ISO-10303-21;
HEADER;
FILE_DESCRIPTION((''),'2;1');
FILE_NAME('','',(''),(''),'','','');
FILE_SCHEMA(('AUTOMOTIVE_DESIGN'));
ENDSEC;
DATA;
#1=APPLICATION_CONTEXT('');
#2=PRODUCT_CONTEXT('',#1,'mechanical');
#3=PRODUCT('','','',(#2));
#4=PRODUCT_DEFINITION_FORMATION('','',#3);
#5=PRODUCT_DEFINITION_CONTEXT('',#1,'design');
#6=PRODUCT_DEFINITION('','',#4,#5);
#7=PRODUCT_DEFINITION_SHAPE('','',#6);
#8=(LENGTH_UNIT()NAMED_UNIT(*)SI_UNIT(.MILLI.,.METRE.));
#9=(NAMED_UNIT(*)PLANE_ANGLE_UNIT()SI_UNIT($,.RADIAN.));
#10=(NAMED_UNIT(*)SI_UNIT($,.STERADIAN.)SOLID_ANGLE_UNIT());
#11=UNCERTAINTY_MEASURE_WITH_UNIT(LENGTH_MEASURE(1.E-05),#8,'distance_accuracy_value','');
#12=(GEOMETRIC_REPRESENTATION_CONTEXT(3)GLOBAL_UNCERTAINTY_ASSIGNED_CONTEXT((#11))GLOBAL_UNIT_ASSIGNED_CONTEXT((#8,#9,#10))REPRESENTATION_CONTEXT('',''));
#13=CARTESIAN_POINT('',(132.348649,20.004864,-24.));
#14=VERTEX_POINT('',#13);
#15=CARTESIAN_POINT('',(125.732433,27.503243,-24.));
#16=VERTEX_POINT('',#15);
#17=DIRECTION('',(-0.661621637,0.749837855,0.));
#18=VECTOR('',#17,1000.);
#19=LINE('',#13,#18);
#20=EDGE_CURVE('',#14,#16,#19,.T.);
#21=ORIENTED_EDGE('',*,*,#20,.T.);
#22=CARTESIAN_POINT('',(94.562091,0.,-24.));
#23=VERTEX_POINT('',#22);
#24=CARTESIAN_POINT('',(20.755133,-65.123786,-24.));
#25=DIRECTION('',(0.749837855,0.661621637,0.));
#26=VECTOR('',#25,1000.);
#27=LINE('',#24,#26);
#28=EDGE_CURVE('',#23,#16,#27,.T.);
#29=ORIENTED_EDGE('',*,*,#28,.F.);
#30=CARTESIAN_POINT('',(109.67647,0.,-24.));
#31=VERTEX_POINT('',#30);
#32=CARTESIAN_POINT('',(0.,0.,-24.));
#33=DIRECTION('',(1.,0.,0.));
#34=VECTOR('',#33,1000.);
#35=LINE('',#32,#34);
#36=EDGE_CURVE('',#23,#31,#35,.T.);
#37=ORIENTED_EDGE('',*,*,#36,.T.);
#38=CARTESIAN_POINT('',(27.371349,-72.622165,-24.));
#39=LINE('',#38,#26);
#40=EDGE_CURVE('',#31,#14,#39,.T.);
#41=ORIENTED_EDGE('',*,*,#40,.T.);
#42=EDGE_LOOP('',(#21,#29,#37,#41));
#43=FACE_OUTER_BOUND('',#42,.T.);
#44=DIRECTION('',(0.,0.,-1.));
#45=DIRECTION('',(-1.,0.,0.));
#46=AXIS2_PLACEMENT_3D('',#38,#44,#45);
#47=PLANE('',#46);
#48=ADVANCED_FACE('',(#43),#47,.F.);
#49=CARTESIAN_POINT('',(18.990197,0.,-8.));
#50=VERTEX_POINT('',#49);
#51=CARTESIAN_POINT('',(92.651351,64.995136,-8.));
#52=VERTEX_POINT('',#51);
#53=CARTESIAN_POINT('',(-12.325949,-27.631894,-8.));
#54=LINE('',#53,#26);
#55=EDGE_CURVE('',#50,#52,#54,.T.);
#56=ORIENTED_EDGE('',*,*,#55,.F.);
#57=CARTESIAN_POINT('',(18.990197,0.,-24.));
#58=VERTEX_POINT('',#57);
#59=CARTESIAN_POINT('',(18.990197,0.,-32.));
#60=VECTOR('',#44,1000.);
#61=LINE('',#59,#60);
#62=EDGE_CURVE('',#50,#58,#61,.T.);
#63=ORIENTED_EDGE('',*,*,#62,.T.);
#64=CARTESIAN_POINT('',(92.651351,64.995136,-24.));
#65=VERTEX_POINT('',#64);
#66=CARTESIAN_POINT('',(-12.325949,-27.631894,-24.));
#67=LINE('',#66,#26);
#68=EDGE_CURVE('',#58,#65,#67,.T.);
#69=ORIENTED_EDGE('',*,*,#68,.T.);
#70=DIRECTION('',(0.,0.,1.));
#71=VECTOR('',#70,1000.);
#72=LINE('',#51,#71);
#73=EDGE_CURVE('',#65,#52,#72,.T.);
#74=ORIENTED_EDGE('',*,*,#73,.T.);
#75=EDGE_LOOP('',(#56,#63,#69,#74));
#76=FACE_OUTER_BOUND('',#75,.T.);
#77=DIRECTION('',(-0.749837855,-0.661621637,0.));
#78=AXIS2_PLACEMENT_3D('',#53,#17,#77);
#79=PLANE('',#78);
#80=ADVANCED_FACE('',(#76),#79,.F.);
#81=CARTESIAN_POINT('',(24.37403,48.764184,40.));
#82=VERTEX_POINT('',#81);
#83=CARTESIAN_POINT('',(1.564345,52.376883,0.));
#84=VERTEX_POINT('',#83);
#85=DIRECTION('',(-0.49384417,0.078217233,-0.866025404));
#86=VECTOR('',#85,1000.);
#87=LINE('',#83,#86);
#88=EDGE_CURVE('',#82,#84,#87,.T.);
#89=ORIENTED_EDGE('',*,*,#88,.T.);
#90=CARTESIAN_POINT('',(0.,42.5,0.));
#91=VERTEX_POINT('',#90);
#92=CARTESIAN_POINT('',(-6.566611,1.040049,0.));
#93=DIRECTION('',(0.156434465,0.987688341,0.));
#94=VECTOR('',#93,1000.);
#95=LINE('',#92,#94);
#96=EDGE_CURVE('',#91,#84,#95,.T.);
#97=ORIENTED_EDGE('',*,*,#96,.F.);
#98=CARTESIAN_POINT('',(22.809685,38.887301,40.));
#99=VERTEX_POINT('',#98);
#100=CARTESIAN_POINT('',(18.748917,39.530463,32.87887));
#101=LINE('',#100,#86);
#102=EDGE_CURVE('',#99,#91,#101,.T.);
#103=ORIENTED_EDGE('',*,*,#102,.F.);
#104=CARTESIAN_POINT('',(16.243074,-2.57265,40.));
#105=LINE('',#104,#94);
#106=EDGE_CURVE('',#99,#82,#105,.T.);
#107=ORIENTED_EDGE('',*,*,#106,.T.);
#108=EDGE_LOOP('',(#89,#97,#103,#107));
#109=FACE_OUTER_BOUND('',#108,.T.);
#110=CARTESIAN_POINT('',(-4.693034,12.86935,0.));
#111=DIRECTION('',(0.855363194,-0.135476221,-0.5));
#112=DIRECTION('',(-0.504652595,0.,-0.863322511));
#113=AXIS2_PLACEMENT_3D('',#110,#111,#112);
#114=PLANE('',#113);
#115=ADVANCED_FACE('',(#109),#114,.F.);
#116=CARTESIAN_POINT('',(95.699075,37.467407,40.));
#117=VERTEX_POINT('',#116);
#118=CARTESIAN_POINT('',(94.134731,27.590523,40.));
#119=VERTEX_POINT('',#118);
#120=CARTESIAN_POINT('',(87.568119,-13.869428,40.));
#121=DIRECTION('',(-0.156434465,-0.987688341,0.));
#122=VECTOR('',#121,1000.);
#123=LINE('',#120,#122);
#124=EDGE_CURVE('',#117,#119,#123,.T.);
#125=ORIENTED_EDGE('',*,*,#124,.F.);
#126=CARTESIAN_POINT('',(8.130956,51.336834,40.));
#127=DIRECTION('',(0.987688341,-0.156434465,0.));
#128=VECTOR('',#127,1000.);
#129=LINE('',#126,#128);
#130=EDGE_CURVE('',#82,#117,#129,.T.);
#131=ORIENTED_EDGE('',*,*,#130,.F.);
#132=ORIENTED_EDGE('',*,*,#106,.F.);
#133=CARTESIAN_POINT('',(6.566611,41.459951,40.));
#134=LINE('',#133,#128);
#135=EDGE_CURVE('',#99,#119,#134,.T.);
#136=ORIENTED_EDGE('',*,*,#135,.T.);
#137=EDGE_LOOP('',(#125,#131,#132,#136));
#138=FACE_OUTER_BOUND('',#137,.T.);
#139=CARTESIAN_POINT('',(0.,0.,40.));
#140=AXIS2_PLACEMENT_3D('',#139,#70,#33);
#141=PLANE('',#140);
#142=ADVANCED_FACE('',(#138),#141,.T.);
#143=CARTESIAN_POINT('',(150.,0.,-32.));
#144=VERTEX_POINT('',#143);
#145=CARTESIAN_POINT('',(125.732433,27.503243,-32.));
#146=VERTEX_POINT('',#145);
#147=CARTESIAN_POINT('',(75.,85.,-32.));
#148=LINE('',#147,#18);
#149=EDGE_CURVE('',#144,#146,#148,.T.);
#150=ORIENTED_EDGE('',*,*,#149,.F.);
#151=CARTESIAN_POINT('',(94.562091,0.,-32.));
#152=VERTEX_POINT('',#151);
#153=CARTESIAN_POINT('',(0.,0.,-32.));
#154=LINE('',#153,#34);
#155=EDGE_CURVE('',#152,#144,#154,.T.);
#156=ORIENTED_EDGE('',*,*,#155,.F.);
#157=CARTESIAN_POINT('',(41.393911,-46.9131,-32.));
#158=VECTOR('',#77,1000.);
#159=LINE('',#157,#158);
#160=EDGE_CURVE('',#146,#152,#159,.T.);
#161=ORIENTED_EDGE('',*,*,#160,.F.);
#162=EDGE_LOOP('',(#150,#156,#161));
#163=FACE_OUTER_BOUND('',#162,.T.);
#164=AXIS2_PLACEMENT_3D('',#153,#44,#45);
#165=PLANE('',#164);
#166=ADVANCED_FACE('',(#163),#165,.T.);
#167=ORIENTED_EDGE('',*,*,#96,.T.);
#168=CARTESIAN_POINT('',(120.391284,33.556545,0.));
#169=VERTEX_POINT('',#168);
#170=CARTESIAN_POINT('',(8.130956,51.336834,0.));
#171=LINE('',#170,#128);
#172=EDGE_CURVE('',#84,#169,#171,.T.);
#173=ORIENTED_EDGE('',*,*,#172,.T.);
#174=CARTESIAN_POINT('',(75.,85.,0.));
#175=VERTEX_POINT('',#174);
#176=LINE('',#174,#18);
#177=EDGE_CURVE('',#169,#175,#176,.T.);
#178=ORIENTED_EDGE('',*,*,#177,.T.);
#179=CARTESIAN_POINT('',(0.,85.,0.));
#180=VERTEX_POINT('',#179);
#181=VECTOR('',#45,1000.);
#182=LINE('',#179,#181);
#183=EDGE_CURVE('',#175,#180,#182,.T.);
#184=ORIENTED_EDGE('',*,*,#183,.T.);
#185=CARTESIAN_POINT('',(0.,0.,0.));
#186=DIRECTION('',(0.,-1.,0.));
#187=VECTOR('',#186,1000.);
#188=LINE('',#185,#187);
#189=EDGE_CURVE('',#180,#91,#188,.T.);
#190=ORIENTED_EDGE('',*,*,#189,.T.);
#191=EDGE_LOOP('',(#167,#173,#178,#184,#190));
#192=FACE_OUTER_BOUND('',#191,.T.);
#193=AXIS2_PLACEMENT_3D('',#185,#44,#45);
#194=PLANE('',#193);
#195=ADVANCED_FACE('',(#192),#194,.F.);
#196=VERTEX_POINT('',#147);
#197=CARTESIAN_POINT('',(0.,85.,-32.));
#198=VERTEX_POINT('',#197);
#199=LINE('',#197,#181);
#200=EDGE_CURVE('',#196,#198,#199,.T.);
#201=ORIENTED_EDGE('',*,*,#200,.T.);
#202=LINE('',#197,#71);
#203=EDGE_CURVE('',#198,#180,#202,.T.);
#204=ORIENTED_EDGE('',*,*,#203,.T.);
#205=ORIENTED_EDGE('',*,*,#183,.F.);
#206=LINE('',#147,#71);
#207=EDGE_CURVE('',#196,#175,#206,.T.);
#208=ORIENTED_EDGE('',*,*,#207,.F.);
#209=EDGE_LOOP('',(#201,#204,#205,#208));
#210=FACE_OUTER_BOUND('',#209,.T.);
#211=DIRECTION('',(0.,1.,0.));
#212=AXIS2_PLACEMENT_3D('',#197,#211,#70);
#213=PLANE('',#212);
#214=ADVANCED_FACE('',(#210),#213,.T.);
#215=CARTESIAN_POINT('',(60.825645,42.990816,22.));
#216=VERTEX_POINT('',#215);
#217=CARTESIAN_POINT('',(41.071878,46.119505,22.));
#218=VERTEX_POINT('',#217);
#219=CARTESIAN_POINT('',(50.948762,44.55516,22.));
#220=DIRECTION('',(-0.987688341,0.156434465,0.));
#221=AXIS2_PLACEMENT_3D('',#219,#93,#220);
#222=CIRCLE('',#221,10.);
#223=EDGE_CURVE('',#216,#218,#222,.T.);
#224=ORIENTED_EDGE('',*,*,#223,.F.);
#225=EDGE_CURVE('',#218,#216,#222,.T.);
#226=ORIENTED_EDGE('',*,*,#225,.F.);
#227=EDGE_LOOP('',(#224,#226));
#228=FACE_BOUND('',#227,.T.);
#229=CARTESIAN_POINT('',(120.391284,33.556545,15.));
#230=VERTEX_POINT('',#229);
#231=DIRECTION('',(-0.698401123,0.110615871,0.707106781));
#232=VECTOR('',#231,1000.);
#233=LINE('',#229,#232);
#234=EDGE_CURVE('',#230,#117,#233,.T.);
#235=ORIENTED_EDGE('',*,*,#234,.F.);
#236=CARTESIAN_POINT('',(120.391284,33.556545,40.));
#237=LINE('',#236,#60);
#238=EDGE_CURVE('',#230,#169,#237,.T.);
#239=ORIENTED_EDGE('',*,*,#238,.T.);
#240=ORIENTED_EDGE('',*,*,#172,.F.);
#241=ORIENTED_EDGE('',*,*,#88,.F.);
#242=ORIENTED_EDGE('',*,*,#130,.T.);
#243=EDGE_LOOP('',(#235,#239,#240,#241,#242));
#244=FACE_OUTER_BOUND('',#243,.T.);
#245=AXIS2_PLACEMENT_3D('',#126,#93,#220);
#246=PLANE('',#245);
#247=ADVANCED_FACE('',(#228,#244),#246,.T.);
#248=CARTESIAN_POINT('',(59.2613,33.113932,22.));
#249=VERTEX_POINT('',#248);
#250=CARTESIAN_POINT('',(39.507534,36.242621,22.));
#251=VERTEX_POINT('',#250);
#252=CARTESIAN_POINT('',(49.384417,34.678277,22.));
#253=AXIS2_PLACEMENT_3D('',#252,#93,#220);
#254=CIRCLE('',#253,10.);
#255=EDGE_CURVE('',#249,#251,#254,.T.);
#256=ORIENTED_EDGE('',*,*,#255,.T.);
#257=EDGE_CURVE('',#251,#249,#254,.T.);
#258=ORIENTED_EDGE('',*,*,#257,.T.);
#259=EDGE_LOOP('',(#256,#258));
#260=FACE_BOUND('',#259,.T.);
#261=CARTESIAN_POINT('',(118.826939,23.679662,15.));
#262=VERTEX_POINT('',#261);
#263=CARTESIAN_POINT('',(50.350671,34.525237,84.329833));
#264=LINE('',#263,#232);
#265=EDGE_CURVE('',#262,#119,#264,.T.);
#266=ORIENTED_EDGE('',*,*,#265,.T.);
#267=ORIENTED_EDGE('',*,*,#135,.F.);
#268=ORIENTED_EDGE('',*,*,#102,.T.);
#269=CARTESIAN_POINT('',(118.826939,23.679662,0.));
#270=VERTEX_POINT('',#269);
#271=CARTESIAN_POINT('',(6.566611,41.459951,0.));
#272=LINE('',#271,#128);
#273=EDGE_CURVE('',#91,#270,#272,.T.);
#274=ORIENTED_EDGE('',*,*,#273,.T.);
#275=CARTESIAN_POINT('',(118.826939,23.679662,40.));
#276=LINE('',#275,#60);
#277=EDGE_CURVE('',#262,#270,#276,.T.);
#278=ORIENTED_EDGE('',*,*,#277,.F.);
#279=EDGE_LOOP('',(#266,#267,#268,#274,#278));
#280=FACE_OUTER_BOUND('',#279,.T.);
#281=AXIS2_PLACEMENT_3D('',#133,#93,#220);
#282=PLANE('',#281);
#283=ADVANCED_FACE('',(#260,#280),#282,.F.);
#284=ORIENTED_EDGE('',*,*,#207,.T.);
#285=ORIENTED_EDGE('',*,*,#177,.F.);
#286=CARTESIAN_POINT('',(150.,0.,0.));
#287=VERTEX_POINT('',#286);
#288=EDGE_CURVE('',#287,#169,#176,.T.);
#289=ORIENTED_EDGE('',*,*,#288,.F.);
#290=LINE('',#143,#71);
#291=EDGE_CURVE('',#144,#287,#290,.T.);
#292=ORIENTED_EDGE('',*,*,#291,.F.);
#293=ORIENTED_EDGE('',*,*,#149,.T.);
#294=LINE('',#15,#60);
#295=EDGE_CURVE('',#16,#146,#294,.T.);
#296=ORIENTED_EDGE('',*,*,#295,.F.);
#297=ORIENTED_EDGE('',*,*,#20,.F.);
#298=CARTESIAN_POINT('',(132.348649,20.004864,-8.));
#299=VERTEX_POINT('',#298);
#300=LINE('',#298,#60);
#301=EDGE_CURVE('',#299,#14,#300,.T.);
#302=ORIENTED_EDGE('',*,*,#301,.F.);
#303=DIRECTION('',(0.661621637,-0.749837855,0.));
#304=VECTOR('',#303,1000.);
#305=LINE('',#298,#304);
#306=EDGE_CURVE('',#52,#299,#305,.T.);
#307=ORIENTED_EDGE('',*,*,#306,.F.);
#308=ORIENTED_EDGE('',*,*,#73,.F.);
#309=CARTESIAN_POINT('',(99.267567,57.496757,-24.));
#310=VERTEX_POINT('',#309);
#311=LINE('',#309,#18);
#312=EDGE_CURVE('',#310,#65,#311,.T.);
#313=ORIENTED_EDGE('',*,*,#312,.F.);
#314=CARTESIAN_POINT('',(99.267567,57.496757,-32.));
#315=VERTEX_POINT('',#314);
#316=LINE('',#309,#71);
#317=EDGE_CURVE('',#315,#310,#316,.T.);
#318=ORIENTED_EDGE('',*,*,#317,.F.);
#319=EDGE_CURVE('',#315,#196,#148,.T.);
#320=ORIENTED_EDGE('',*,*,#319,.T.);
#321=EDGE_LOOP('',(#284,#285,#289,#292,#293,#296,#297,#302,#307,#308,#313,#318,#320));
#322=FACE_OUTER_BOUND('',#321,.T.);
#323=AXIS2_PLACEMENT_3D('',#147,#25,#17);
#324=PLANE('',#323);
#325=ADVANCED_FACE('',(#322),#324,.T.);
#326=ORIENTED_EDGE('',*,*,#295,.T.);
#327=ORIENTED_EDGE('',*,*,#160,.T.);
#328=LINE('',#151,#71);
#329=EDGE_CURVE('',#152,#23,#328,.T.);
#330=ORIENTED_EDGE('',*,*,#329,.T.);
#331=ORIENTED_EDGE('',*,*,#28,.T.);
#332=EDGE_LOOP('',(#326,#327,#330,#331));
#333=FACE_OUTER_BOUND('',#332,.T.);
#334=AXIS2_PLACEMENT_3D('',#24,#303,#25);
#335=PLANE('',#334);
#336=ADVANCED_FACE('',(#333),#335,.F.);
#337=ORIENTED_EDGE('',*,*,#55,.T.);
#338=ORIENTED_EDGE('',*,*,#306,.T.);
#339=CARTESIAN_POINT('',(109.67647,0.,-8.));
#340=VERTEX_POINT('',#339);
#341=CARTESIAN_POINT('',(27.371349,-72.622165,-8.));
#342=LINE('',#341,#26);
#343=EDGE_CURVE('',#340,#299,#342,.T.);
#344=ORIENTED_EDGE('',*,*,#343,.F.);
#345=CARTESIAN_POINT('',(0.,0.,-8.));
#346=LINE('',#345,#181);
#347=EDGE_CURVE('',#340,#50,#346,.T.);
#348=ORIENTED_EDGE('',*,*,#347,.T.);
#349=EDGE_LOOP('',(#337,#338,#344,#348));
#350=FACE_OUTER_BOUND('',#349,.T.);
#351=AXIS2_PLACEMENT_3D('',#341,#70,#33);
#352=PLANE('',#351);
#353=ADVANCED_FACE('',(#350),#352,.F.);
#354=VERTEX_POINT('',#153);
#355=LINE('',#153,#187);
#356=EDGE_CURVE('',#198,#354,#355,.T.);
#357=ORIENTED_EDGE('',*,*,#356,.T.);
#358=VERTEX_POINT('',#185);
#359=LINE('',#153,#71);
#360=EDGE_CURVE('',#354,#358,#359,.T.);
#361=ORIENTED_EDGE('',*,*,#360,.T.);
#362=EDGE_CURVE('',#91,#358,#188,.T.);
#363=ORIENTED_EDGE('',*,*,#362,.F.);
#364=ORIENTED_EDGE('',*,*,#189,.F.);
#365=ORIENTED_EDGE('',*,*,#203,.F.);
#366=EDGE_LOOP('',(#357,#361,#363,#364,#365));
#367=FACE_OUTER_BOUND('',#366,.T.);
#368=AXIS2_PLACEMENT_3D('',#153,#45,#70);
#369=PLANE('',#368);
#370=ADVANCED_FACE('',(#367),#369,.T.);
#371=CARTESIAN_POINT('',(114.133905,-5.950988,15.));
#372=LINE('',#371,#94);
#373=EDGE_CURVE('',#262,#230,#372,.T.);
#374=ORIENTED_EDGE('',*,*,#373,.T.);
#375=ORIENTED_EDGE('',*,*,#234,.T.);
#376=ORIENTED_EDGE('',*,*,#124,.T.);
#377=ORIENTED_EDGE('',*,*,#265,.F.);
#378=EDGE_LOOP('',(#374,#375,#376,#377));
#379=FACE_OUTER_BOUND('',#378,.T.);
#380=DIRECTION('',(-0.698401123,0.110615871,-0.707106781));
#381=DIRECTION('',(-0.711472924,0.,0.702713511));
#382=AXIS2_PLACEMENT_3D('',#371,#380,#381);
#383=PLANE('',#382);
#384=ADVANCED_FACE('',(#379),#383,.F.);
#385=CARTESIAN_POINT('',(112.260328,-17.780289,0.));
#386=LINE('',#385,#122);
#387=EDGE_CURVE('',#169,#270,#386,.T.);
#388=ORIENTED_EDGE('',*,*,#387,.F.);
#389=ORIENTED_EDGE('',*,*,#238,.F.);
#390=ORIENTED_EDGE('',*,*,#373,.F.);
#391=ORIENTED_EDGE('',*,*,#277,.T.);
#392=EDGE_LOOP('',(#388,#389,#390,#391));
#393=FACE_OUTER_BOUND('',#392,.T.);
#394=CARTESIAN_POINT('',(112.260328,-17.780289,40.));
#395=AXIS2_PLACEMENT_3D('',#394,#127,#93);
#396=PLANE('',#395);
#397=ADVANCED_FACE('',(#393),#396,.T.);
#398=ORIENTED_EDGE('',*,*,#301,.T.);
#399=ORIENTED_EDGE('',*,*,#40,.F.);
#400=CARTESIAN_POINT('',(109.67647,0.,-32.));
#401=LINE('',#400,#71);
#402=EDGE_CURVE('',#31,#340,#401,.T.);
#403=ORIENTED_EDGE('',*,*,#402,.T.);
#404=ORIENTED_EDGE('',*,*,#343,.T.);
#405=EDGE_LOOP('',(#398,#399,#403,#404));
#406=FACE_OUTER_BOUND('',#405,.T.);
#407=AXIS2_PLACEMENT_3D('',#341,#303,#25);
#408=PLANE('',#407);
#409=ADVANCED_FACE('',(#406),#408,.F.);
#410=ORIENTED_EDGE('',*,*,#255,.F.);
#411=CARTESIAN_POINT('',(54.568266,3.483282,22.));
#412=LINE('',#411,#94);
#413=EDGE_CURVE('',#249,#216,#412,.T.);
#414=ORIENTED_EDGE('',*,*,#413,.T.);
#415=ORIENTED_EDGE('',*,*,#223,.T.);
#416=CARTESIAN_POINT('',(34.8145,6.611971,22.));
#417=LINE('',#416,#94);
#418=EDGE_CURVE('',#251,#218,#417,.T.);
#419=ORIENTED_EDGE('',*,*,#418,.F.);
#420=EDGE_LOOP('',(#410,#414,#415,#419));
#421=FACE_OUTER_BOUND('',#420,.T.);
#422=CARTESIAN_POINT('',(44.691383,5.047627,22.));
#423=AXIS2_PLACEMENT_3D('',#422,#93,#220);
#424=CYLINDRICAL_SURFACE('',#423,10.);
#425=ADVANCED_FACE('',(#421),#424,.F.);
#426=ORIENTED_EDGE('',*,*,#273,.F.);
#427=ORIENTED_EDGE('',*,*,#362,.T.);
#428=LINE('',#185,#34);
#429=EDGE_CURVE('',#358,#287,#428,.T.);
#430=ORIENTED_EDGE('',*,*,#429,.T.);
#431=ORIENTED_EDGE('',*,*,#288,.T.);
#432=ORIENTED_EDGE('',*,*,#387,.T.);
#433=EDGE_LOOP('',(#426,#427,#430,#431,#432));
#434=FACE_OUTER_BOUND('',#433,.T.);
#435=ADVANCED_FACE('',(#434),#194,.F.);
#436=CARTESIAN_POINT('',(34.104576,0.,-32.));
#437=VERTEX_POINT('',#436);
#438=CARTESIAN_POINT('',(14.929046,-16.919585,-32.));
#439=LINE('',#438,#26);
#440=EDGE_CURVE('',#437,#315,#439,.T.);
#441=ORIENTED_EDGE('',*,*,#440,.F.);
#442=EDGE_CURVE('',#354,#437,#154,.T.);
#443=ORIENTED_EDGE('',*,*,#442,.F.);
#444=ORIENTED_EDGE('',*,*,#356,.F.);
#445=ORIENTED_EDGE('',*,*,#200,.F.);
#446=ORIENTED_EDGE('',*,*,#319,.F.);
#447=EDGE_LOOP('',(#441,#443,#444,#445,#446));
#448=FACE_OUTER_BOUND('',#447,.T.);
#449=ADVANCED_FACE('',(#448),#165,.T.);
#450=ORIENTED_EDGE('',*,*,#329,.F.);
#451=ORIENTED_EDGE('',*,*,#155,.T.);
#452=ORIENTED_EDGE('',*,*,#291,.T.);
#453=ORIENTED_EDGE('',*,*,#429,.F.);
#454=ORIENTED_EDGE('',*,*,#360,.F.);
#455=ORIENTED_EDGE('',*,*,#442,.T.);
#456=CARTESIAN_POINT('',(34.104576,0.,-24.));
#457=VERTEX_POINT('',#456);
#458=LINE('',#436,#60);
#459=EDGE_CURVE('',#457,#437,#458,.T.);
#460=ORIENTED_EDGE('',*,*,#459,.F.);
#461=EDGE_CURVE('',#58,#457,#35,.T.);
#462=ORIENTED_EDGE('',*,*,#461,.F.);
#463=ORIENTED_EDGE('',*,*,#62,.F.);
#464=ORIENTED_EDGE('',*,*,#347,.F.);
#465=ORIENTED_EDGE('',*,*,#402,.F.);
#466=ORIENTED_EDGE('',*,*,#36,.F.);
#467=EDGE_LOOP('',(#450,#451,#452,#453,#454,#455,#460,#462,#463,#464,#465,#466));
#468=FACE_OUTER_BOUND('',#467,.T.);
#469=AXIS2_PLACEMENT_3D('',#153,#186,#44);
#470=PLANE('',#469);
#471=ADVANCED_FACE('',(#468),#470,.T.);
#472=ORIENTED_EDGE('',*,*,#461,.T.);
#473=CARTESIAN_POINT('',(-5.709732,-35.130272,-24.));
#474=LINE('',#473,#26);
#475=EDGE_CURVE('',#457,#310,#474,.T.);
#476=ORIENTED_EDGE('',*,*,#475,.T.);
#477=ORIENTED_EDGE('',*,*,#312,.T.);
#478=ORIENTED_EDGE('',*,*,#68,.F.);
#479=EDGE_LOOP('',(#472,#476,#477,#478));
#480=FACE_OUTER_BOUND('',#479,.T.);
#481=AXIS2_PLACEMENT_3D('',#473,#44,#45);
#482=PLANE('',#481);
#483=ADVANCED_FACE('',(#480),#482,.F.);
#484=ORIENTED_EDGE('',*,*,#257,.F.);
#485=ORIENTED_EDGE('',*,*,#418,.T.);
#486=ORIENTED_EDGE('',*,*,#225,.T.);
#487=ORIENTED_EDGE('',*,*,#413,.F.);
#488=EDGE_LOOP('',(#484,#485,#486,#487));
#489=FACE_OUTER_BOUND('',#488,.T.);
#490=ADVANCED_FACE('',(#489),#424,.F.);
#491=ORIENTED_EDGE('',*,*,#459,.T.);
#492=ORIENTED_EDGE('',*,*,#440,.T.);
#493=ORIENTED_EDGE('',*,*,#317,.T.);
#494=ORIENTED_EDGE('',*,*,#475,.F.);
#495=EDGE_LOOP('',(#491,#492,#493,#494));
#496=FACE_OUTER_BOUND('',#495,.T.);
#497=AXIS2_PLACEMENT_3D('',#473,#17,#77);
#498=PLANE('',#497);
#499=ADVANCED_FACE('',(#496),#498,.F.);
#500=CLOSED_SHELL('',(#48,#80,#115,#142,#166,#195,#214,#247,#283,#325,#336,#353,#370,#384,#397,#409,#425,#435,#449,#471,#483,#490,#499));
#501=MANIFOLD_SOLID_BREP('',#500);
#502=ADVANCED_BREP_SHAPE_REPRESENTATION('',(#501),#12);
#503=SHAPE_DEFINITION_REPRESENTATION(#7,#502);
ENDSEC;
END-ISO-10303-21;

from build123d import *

# Parameters (mm, degrees)
BASE_BLOCK_DEPTH       = 32
SLOT_CUT_DEPTH         = 140
ANGLED_WING_DEPTH      = 40
WING_TRIM_CUT_SKETCH_R = 10
WING_TRIM_CUT_DEPTH    = 40


with BuildPart() as part:
    # Base Block Sketch → Base Block (new body)
    with BuildSketch(Plane.XY):
        Polygon((75, 85), (150, 0), (0, 0), (0, 85), align=None)
    extrude(amount=-BASE_BLOCK_DEPTH)

    # Slot Cut Sketch → Slot Cut (cut)
    with BuildSketch(Plane(origin=(84.338521401, 74.416342412, 0), x_dir=(0, 0, -1), z_dir=(0.7498378553650925, 0.6616216370868463, 0))):
        Polygon((24, -22.564325319), (32, -22.564325319), (32, -62.564325319), (24, -62.564325319), (24, -72.564325319), (8, -72.564325319), (8, -12.564325319), (24, -12.564325319), align=None)
    extrude(amount=-SLOT_CUT_DEPTH, mode=Mode.SUBTRACT)

    # Angled Wing Sketch → Angled Wing (add)
    with BuildSketch(Plane.XY):
        Polygon((120.39128367, 33.556545174), (118.82693902, 23.679661768), (0, 42.5), (1.56434465, 52.376883406), align=None)
    extrude(amount=ANGLED_WING_DEPTH)

    # Wing Trim Cut Sketch → Wing Trim Cut (cut)
    with BuildSketch(Plane(origin=(8.130955781, 51.336834377, 0), x_dir=(0.9876883405951389, -0.15643446504022435, 0), z_dir=(0.15643446504022435, 0.9876883405951389, 0))):
        with Locations(Location((43.351535236, -22, 0), (0, 0, 180))):
            Circle(WING_TRIM_CUT_SKETCH_R)
        Polygon((-6.648464764, 0), (20.17251839, -46.455305531), (-6.648464764, -46.455305531), align=None)
        Polygon((113.659666997, -15), (81.480803865, -47.178863132), (138.076260789, -47.178863132), align=None)
    extrude(amount=-WING_TRIM_CUT_DEPTH, mode=Mode.SUBTRACT)


solid = part.part
